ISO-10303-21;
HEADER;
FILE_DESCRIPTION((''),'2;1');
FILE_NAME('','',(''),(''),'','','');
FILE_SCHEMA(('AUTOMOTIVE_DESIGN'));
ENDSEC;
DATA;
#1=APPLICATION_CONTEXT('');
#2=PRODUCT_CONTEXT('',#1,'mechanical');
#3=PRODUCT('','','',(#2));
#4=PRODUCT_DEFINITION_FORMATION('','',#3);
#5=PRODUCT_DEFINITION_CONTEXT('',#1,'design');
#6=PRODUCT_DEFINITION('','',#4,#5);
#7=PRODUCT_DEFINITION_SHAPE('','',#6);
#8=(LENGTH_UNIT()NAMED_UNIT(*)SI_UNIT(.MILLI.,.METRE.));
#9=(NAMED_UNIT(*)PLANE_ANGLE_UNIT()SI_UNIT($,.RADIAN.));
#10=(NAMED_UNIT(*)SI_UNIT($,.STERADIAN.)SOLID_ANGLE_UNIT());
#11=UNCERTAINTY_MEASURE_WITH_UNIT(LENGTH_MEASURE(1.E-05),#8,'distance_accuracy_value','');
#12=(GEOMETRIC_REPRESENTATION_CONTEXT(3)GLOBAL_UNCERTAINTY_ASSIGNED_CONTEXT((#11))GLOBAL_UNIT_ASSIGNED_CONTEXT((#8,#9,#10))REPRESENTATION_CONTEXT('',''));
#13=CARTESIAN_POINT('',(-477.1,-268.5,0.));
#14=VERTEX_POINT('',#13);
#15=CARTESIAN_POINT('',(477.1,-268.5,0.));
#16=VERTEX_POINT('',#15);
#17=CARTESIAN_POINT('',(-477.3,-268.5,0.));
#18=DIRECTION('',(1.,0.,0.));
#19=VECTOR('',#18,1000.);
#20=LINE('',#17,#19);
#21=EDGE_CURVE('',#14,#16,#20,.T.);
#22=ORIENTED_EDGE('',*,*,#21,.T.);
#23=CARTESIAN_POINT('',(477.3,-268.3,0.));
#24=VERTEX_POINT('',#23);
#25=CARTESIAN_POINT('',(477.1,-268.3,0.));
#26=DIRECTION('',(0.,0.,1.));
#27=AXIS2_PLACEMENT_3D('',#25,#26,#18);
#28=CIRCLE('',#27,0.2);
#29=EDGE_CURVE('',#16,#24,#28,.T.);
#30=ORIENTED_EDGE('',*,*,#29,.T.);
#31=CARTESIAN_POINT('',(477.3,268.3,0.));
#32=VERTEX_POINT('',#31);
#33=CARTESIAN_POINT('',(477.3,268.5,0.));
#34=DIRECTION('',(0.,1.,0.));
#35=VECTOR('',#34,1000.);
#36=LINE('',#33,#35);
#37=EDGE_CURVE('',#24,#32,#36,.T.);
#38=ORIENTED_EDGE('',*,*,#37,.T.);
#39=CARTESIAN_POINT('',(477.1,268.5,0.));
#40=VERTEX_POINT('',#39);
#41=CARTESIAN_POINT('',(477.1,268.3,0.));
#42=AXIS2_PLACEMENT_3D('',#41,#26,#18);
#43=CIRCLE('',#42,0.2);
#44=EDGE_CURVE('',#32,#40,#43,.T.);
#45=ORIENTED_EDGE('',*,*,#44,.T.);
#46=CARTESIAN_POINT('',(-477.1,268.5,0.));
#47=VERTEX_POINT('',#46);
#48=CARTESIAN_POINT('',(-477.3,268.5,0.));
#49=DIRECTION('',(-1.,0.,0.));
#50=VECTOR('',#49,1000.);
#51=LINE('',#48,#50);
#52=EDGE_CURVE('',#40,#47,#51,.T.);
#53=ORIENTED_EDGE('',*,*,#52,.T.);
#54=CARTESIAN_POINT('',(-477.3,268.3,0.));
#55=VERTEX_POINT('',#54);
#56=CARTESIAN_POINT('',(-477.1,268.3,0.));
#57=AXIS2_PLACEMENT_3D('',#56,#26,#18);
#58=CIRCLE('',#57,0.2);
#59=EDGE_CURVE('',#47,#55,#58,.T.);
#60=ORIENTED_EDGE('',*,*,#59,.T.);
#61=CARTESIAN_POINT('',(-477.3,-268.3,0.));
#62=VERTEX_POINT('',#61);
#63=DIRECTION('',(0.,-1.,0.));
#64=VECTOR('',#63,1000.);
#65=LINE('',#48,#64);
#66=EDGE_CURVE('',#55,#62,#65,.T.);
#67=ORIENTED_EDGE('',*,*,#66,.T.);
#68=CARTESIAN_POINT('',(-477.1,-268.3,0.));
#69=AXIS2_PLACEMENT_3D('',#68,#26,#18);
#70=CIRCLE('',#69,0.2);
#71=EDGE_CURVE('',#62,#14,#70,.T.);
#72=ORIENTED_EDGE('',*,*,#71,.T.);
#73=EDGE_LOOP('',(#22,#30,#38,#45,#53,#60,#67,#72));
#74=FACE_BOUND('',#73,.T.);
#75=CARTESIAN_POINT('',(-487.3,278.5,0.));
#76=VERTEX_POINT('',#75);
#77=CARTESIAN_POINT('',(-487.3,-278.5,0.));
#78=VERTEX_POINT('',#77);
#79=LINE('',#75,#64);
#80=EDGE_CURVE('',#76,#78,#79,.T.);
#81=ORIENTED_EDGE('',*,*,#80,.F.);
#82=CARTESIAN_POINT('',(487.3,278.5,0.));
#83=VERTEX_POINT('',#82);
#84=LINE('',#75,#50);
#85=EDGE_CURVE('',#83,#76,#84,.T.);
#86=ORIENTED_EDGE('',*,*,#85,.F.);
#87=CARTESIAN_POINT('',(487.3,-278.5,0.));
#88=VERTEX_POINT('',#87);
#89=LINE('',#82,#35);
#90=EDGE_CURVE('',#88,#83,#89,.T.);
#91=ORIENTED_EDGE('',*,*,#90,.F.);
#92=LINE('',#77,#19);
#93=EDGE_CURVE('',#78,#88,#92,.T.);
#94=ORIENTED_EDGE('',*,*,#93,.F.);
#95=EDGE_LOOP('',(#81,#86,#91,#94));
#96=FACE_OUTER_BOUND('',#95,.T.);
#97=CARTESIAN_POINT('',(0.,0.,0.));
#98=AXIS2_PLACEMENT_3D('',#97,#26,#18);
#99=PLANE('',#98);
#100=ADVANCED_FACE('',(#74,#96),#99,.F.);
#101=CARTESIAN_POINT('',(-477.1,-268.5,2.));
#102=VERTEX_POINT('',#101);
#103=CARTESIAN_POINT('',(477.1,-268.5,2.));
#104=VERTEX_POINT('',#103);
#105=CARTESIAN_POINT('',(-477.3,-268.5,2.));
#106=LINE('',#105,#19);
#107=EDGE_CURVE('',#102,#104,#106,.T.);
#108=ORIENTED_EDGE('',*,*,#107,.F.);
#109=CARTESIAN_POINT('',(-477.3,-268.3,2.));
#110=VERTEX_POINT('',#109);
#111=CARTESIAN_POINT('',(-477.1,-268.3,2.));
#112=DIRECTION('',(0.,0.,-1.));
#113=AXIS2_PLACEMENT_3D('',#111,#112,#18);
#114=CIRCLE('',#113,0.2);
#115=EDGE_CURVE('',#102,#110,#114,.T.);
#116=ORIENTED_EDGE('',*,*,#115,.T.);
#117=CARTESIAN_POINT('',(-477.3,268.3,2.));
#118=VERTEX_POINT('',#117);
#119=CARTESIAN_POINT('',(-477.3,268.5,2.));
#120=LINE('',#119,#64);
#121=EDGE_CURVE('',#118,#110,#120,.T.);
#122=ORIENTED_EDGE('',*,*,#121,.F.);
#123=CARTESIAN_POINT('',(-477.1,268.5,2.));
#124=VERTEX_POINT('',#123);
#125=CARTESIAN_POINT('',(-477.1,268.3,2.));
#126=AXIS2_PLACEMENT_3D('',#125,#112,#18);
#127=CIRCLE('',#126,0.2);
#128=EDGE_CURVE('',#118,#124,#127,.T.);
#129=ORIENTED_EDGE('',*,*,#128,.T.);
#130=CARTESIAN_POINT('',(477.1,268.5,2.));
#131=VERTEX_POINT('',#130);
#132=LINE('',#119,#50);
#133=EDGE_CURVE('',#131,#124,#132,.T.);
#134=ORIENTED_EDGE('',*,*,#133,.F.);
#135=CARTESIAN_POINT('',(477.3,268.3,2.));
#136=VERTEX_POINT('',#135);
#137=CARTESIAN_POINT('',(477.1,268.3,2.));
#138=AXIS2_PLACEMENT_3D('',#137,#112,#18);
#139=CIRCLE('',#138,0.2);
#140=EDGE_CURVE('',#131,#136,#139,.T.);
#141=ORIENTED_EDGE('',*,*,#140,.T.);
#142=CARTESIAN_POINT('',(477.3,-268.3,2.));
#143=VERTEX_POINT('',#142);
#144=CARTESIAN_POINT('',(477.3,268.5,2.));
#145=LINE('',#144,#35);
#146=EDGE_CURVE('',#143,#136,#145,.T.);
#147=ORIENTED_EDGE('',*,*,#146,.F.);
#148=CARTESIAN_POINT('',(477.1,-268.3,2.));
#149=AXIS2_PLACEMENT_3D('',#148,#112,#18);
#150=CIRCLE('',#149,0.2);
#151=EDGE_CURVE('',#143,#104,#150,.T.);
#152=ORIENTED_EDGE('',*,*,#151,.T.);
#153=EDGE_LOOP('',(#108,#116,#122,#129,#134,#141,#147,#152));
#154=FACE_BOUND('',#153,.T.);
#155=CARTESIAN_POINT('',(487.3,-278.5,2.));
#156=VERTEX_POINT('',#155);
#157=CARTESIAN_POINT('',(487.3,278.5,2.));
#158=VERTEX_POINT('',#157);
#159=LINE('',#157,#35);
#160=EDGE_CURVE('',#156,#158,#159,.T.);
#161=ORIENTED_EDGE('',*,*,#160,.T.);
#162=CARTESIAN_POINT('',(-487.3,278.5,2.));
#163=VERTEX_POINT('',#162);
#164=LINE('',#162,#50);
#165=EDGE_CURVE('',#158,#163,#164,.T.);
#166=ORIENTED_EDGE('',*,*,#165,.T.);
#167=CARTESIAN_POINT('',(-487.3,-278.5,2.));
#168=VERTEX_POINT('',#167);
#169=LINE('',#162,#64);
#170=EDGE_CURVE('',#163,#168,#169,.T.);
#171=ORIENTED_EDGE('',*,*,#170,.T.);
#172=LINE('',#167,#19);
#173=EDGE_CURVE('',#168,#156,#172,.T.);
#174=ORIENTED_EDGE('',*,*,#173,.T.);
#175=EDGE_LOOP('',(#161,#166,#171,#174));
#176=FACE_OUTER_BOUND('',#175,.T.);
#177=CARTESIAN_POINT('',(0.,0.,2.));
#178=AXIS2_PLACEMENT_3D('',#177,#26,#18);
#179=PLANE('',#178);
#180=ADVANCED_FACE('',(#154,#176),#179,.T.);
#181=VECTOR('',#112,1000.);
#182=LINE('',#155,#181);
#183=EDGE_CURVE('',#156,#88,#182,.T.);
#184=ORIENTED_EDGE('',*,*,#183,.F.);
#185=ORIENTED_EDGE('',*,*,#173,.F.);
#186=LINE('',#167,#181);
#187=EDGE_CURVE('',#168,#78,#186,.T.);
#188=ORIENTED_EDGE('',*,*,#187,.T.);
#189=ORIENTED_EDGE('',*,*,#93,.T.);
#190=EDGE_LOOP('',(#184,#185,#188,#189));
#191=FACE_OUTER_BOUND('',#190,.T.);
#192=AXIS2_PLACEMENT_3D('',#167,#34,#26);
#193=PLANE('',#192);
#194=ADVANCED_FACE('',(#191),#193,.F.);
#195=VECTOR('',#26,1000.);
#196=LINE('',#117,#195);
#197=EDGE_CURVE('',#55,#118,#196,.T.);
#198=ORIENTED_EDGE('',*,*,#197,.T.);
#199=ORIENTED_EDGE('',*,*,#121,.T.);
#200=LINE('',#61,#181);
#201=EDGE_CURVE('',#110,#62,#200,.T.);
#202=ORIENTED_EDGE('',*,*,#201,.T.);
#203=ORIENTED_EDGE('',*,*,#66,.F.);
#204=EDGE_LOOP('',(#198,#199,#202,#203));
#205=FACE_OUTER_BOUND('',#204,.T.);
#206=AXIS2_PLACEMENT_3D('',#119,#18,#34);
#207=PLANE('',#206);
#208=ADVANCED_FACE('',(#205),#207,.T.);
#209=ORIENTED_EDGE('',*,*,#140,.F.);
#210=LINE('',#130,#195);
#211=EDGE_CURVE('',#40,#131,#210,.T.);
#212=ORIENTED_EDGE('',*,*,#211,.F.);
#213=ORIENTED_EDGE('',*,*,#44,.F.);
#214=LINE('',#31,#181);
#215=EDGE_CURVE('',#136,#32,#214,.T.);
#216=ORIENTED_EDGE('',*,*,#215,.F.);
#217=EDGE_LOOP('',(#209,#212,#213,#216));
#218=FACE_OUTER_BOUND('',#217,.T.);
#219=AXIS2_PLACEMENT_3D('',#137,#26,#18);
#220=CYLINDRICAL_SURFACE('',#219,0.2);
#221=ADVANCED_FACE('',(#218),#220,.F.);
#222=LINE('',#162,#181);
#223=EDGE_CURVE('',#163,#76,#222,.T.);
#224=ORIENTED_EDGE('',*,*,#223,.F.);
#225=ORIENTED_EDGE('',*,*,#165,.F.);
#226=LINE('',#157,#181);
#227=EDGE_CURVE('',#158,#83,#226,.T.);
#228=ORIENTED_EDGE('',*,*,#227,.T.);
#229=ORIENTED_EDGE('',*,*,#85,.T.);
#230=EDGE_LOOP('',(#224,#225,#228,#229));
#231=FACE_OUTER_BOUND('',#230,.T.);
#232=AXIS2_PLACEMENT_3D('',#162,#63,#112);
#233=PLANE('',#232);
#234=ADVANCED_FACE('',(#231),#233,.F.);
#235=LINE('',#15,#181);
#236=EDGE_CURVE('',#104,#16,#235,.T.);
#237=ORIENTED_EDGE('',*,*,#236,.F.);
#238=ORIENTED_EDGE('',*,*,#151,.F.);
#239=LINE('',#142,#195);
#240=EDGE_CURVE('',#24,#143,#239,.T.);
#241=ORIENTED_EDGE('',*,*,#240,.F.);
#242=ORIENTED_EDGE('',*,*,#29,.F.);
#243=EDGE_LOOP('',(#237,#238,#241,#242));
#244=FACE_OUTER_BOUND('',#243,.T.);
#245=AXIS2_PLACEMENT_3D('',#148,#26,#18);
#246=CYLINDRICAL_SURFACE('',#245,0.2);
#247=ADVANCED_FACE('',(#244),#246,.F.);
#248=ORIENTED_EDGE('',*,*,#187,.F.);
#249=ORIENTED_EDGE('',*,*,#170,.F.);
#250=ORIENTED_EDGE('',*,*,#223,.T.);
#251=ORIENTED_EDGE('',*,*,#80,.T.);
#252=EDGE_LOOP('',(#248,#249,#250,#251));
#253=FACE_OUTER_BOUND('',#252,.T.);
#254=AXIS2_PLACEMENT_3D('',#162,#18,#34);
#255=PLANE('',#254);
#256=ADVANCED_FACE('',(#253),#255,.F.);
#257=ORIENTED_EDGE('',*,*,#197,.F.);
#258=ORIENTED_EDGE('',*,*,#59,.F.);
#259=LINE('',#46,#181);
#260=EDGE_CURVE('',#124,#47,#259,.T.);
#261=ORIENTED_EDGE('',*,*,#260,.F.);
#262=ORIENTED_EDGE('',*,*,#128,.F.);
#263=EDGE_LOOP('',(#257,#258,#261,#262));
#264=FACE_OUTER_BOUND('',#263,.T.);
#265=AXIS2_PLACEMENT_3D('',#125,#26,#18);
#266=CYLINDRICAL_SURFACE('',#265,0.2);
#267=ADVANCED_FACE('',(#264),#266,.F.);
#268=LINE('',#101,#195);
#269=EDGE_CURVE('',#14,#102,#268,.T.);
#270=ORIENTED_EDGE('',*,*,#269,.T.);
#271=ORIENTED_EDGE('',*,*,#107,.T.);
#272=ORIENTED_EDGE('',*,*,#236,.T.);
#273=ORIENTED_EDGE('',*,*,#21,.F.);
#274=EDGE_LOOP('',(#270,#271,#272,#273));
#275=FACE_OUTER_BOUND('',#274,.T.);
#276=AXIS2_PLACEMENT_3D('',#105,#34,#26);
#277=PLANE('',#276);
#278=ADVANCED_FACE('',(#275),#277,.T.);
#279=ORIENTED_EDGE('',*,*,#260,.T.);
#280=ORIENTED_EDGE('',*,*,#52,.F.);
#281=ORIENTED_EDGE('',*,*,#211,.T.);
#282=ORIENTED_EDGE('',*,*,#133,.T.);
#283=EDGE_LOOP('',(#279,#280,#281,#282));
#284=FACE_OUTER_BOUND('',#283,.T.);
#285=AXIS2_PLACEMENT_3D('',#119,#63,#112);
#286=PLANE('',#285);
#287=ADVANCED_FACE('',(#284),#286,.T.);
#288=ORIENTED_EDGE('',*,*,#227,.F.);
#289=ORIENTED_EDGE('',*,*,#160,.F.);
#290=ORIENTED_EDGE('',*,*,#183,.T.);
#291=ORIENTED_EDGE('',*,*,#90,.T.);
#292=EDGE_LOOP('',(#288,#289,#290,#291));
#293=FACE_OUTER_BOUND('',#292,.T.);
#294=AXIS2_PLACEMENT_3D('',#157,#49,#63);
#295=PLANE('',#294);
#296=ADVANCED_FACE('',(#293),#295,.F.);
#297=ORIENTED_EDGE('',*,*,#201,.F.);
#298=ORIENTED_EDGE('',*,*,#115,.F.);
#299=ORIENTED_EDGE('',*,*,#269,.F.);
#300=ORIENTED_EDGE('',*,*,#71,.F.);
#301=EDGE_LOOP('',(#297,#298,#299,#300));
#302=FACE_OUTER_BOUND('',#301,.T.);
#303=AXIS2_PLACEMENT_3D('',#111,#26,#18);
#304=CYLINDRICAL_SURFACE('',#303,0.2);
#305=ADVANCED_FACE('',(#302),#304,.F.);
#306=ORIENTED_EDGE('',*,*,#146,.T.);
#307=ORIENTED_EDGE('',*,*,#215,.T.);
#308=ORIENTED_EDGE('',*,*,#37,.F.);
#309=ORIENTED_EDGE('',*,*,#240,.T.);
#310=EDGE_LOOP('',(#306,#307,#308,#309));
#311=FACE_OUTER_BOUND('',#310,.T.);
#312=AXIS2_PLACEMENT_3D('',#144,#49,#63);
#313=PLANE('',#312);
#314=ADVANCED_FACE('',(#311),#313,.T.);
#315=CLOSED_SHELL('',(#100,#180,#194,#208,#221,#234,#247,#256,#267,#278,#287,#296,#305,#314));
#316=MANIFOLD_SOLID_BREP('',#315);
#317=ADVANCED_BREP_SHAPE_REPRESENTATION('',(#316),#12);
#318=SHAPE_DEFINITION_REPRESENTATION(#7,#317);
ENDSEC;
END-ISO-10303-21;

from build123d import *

# Parameters (mm, degrees)
SKETCH_1_W      = 974.6
SKETCH_1_H      = 557
SKETCH_1_W_2    = 954.6
SKETCH_1_H_2    = 537
EXTRUDE_1_DEPTH = 2
FILLET_1_R      = 0.2


with BuildPart() as part:
    # 草图1 → 凸台-拉伸1 (new body)
    with BuildSketch(Plane.XY):
        Rectangle(SKETCH_1_W, SKETCH_1_H)
        Rectangle(SKETCH_1_W_2, SKETCH_1_H_2, mode=Mode.SUBTRACT)
    extrude(amount=EXTRUDE_1_DEPTH)

    # 圆角1
    fillet_1_edges = [part.edges().sort_by_distance(p)[0] for p in [
        (477.3, -268.5, 1),
        (477.3, 268.5, 1),
        (-477.3, 268.5, 1),
        (-477.3, -268.5, 1),
    ]]
    fillet(fillet_1_edges, radius=FILLET_1_R)


solid = part.part
